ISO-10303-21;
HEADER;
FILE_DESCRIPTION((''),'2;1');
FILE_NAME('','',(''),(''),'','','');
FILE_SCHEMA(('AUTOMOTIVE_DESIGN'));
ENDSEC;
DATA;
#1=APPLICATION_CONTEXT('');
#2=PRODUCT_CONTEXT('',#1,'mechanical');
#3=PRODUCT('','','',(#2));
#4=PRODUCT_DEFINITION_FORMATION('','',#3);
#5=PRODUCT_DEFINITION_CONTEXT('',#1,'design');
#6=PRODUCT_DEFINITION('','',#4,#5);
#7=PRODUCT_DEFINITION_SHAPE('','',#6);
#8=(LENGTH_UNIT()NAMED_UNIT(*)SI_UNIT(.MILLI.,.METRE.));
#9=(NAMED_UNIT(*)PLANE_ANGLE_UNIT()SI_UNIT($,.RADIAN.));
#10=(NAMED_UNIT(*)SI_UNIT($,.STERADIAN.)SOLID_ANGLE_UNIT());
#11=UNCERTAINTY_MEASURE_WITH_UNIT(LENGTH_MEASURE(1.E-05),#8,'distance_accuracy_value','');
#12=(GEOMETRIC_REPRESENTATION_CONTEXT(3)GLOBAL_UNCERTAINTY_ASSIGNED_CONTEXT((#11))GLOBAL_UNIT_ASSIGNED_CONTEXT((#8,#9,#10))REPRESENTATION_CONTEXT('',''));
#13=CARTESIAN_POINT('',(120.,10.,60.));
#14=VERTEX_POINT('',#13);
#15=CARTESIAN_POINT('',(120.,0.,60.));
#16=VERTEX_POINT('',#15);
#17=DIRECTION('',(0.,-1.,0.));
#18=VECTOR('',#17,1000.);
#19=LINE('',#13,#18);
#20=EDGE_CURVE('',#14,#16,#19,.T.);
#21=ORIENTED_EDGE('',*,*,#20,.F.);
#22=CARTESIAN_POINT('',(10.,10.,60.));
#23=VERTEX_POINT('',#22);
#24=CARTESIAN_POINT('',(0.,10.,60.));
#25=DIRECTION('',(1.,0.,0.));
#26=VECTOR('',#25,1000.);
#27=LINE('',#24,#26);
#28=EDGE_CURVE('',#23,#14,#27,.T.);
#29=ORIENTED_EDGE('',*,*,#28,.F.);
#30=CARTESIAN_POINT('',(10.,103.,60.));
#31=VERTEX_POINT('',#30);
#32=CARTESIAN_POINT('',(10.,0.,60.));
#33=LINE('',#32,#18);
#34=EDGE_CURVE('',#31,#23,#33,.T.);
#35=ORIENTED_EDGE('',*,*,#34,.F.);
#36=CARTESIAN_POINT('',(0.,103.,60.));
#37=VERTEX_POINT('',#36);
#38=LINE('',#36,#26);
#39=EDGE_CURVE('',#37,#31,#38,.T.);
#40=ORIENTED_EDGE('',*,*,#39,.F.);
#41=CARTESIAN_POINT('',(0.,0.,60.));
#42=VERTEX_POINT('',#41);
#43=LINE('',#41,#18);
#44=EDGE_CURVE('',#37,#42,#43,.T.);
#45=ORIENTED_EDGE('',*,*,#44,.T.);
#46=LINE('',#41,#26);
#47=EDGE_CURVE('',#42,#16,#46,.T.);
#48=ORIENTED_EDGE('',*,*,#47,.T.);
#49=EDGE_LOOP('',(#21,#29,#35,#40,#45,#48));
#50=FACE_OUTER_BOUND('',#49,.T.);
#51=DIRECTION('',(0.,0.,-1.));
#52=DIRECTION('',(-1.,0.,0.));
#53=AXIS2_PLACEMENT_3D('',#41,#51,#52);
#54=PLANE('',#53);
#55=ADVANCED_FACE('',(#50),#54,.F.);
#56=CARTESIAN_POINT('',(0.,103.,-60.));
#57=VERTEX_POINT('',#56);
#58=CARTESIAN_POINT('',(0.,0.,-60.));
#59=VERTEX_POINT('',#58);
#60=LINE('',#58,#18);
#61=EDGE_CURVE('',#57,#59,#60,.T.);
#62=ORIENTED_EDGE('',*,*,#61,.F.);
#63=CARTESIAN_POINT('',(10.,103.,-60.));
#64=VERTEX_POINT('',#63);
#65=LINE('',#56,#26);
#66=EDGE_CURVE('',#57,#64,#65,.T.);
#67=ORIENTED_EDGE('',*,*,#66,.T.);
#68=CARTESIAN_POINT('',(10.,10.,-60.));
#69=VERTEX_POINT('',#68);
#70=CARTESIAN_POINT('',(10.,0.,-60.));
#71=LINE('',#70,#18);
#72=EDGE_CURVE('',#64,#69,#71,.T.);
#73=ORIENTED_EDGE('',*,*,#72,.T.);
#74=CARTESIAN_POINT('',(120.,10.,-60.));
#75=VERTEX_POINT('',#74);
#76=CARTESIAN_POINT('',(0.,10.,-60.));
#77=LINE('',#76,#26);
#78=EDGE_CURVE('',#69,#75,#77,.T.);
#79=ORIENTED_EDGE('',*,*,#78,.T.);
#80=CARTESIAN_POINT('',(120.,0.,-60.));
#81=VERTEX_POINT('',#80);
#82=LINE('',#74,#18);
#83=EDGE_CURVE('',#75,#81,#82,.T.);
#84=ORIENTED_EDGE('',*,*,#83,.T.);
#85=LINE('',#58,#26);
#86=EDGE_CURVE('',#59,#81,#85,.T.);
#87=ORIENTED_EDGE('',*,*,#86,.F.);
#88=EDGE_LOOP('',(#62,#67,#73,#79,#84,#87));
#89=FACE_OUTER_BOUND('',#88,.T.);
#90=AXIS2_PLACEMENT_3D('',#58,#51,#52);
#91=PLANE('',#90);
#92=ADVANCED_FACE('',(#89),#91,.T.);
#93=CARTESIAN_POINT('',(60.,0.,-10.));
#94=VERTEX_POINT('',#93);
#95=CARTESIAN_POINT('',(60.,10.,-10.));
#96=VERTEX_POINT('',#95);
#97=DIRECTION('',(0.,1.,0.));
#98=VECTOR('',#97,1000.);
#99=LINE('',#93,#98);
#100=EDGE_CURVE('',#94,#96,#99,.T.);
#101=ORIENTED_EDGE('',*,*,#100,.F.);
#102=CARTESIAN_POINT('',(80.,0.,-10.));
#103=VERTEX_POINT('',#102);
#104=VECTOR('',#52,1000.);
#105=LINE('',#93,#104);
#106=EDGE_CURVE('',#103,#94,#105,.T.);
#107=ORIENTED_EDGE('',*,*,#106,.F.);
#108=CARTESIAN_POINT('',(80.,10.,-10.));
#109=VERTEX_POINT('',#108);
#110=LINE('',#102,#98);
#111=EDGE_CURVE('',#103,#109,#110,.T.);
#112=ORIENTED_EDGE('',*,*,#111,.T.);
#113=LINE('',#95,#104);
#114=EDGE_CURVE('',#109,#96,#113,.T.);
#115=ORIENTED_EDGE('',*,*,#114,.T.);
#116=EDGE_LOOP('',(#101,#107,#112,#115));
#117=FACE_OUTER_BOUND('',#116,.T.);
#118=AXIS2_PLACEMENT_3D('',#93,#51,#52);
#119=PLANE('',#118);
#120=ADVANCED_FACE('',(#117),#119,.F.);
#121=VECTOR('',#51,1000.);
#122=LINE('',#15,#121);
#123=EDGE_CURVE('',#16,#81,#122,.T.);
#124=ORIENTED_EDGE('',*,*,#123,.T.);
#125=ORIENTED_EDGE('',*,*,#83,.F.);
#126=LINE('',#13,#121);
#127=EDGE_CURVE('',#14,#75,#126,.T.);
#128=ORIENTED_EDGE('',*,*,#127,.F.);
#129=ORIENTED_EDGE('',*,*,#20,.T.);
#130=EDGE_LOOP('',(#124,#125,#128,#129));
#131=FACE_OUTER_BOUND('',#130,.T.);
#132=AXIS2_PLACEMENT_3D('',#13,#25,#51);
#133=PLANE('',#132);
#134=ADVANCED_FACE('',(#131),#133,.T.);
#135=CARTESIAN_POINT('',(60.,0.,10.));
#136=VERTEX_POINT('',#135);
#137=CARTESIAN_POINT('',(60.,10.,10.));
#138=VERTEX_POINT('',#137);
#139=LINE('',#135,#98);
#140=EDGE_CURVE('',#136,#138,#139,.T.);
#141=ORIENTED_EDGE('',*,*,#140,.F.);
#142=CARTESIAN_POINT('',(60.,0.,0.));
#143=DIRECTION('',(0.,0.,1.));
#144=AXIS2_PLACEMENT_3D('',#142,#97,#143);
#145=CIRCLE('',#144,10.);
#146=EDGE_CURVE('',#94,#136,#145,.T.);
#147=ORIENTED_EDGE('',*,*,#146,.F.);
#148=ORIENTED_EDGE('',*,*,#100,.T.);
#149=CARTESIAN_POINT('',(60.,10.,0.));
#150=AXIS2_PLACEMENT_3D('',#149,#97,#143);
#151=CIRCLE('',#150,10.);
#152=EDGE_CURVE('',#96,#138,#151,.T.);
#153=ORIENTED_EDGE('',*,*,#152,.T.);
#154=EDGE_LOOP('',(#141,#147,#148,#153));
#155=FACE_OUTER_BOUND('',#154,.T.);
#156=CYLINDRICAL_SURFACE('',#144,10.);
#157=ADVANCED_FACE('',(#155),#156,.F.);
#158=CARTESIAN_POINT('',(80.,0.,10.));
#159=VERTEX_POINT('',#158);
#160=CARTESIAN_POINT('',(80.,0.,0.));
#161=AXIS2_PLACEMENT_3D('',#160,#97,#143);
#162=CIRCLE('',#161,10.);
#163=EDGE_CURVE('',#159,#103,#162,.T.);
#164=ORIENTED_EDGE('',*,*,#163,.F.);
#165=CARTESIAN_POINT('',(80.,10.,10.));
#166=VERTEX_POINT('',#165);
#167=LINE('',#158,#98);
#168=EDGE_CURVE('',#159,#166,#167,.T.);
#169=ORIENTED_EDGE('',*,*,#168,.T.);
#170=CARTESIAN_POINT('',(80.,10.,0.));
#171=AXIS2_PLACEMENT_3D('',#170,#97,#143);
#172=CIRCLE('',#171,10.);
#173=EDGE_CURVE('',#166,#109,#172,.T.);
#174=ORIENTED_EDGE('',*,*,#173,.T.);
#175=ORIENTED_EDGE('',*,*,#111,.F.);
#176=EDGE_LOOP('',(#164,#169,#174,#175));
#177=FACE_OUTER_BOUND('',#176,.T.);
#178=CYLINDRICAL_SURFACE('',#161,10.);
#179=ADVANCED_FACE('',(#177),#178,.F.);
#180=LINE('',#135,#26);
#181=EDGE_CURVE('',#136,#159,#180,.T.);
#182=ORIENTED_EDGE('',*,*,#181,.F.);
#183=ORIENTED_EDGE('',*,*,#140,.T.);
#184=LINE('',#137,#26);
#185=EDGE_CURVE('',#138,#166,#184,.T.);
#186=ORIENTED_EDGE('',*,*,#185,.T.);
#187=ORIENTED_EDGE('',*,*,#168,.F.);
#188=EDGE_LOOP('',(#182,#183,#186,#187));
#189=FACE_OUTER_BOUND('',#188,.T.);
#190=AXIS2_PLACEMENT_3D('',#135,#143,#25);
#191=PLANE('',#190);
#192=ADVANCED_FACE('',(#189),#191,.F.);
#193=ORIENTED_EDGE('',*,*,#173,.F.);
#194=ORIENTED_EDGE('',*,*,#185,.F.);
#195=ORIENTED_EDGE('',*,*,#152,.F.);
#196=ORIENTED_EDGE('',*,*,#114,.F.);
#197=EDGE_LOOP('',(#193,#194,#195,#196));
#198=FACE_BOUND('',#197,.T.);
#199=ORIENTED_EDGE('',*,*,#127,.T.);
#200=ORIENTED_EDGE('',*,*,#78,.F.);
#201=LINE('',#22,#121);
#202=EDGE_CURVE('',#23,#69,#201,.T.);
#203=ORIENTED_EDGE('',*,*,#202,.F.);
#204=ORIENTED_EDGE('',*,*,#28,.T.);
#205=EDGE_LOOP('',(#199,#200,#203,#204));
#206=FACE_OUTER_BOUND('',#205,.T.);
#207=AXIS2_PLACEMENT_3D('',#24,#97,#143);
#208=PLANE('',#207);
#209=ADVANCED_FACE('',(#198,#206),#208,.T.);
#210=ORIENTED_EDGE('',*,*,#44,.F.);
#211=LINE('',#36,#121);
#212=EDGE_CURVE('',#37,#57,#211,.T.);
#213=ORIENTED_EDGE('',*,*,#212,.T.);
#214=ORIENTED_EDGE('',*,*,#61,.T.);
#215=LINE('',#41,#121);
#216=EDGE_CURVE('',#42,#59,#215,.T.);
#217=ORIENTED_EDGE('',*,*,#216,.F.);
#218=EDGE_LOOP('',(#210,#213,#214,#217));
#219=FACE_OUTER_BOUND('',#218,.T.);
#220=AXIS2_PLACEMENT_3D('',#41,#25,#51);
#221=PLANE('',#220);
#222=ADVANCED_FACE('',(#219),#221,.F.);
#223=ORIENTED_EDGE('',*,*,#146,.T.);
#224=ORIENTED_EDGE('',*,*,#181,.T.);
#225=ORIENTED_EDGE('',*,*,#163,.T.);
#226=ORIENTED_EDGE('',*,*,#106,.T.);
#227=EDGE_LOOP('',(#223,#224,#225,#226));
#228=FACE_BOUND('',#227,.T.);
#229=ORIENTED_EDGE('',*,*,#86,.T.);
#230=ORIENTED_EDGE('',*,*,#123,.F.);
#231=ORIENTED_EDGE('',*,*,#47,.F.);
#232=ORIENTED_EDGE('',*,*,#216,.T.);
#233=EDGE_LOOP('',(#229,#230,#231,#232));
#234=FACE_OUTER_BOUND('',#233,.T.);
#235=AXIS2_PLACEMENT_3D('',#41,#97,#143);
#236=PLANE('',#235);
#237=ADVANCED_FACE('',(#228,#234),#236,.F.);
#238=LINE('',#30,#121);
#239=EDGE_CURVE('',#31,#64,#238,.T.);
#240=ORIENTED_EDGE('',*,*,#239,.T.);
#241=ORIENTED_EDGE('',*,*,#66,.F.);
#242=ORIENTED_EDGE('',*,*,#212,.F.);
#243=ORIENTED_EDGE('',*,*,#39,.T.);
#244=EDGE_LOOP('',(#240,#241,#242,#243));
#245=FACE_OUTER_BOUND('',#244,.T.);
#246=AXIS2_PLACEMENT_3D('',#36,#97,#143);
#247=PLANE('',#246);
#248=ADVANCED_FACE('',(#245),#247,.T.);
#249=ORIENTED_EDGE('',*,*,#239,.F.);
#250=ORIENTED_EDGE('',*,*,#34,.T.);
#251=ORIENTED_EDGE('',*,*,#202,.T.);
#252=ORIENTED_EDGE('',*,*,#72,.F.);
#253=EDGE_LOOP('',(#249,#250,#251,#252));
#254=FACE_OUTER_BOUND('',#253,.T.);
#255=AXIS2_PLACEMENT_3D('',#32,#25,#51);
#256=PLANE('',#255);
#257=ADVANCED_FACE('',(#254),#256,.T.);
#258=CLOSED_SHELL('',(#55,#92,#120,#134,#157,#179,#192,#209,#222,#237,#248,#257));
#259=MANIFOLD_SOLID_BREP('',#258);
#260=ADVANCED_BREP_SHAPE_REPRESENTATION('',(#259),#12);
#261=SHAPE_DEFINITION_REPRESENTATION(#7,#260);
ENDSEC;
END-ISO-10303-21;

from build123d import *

# Parameters (mm, degrees)
EXTRUDE_THIN1_DEPTH = 60
CUT_EXTRUDE1_DEPTH  = 164.245214325


with BuildPart() as part:
    # Sketch1 → Extrude-Thin1 (new, symmetric)
    with BuildSketch(Plane.XY):
        Polygon((120, 0), (0, 0), (0, 103), (10, 103), (10, 10), (120, 10), align=None)
    extrude(amount=EXTRUDE_THIN1_DEPTH, both=True)

    # Sketch2 → Cut-Extrude1 (cut, through all)
    with BuildSketch(Plane(origin=(0, 10, 0), x_dir=(1, 0, 0), z_dir=(0, 1, 0))):
        with BuildLine():
            Line((60, 10), (80, 10))
            ThreePointArc((80, 10), (90, 0), (80, -10))
            Line((80, -10), (60, -10))
            ThreePointArc((60, -10), (50, 0), (60, 10))
        make_face()
    extrude(amount=-CUT_EXTRUDE1_DEPTH, mode=Mode.SUBTRACT)


solid = part.part
